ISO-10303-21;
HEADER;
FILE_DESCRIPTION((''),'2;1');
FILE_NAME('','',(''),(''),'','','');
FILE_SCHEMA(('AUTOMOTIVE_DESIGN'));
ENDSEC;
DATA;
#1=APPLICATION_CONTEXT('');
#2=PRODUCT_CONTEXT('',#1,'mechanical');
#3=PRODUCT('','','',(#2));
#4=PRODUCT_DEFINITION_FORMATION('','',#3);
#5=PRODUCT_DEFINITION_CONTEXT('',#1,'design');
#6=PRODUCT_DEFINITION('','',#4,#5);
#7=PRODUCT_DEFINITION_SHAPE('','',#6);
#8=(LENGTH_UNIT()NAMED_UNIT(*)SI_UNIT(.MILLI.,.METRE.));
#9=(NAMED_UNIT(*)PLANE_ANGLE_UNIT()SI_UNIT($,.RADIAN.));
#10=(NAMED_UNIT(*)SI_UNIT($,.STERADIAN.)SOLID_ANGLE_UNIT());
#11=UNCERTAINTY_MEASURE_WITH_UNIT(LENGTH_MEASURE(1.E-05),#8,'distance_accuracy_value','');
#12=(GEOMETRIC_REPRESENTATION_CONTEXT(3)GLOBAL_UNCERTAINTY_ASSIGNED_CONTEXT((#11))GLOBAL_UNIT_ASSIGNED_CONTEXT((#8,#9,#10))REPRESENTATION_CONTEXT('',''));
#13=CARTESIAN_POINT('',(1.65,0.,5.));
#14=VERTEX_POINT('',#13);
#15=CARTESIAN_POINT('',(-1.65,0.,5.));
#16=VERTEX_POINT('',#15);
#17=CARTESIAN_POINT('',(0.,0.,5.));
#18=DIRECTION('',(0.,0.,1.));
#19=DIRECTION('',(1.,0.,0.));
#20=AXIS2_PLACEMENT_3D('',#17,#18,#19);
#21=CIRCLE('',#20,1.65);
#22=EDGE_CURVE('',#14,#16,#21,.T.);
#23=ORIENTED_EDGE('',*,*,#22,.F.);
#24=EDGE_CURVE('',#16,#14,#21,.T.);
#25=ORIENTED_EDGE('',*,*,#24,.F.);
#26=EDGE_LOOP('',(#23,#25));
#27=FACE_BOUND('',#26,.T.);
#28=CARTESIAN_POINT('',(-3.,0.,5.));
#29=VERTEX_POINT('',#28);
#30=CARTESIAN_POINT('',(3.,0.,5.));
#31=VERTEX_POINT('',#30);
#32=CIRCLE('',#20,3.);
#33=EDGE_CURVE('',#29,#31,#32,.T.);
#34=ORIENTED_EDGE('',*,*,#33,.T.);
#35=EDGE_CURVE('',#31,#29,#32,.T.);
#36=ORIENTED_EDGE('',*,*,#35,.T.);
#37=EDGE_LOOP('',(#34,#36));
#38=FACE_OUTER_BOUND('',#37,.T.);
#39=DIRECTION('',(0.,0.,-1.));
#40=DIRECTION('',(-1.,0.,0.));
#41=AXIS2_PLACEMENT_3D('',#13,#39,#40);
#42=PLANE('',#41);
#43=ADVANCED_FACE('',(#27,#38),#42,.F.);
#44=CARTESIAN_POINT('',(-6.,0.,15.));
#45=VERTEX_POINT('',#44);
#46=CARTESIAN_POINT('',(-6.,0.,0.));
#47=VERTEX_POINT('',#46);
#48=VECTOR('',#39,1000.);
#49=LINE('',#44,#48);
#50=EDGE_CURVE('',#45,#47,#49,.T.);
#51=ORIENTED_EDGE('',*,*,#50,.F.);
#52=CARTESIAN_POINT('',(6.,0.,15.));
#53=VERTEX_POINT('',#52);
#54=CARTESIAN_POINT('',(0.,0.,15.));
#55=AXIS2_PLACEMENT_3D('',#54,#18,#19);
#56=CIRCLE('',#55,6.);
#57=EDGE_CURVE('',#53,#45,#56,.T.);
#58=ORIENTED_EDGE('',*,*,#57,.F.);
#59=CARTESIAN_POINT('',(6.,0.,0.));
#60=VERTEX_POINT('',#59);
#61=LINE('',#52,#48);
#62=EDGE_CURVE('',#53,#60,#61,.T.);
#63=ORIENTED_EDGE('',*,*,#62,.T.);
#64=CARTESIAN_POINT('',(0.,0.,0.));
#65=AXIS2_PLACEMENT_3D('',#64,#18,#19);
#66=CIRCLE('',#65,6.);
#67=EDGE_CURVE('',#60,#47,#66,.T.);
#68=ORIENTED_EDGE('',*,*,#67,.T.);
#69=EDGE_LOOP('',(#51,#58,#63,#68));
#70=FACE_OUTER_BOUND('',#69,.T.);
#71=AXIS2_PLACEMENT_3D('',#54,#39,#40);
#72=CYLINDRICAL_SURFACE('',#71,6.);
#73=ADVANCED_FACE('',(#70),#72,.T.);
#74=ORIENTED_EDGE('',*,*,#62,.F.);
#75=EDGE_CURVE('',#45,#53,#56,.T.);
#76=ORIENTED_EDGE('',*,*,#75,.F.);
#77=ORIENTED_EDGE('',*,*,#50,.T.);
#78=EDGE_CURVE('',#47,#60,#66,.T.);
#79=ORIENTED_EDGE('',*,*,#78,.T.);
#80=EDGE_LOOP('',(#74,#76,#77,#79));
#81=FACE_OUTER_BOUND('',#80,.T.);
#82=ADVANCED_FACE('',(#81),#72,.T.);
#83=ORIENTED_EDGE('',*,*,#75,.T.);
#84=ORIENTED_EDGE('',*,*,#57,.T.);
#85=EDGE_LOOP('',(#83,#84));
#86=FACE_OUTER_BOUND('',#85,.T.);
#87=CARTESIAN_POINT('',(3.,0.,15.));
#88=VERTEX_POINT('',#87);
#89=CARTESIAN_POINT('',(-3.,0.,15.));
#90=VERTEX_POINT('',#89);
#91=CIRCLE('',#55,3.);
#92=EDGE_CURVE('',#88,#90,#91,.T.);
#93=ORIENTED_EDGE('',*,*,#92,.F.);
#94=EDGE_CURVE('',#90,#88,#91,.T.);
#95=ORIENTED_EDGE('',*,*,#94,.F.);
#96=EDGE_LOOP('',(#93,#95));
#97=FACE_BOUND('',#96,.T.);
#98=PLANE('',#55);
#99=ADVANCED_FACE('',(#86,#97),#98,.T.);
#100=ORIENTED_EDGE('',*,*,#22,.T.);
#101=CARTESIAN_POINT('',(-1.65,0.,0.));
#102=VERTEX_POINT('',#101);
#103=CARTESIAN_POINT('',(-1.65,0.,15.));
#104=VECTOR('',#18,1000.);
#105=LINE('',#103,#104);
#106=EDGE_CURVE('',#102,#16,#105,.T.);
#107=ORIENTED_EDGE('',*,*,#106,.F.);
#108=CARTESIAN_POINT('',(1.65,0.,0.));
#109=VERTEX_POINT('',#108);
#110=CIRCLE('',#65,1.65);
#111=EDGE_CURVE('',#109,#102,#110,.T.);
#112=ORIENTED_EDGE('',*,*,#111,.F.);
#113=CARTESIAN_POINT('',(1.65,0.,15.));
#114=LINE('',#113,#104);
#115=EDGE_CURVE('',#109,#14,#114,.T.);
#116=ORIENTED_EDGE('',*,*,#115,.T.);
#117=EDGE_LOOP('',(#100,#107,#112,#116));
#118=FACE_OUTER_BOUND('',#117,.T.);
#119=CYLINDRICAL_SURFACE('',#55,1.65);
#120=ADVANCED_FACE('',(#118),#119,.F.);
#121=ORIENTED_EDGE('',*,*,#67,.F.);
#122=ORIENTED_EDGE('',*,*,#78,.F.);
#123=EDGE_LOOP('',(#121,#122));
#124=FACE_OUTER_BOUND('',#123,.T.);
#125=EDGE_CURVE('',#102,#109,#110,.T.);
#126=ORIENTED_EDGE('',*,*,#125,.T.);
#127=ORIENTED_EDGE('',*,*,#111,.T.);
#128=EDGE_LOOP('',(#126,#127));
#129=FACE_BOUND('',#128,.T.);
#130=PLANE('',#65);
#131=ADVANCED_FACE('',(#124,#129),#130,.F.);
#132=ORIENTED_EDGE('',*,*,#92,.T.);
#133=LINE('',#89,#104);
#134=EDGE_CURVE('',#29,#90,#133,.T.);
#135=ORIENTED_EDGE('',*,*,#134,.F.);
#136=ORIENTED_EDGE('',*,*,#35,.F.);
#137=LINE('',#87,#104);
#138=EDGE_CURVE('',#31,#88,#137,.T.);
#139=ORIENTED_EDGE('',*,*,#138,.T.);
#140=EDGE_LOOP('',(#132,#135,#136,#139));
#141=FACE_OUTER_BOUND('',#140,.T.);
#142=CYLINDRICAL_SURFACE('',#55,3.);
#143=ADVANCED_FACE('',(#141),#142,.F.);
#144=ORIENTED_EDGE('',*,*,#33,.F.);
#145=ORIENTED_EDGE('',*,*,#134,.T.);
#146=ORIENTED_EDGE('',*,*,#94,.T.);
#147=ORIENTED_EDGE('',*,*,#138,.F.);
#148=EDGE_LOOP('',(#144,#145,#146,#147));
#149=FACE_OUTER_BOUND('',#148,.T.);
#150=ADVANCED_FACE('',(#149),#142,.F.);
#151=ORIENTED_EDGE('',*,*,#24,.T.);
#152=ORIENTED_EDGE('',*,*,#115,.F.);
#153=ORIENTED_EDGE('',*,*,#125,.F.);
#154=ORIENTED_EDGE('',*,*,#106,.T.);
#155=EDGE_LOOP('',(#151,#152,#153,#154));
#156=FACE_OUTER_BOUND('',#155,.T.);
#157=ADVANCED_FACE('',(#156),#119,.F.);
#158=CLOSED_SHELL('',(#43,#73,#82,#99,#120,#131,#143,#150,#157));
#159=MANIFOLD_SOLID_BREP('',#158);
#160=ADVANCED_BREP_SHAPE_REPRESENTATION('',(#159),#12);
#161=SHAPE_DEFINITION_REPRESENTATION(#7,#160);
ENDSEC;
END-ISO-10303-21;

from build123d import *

# Parameters (mm, degrees)
SKETCH_1_R                = 6
EXTRUDE_1_DEPTH           = 15
HOLE_WIZARD_1_D           = 3.3
HOLE_WIZARD_1_CBORE_D     = 6
HOLE_WIZARD_1_CBORE_DEPTH = 10


with BuildPart() as part:
    # 草图1 → 凸台-拉伸1 (new body)
    with BuildSketch(Plane.XY):
        Circle(SKETCH_1_R)
    extrude(amount=EXTRUDE_1_DEPTH)

    # 打孔尺寸(%根据)内六角圆柱头螺钉的类型1 (through all)
    with Locations(Plane.XY.offset(15)):
        with Locations((0, 0)):
            CounterBoreHole(HOLE_WIZARD_1_D / 2, HOLE_WIZARD_1_CBORE_D / 2, HOLE_WIZARD_1_CBORE_DEPTH)


solid = part.part
